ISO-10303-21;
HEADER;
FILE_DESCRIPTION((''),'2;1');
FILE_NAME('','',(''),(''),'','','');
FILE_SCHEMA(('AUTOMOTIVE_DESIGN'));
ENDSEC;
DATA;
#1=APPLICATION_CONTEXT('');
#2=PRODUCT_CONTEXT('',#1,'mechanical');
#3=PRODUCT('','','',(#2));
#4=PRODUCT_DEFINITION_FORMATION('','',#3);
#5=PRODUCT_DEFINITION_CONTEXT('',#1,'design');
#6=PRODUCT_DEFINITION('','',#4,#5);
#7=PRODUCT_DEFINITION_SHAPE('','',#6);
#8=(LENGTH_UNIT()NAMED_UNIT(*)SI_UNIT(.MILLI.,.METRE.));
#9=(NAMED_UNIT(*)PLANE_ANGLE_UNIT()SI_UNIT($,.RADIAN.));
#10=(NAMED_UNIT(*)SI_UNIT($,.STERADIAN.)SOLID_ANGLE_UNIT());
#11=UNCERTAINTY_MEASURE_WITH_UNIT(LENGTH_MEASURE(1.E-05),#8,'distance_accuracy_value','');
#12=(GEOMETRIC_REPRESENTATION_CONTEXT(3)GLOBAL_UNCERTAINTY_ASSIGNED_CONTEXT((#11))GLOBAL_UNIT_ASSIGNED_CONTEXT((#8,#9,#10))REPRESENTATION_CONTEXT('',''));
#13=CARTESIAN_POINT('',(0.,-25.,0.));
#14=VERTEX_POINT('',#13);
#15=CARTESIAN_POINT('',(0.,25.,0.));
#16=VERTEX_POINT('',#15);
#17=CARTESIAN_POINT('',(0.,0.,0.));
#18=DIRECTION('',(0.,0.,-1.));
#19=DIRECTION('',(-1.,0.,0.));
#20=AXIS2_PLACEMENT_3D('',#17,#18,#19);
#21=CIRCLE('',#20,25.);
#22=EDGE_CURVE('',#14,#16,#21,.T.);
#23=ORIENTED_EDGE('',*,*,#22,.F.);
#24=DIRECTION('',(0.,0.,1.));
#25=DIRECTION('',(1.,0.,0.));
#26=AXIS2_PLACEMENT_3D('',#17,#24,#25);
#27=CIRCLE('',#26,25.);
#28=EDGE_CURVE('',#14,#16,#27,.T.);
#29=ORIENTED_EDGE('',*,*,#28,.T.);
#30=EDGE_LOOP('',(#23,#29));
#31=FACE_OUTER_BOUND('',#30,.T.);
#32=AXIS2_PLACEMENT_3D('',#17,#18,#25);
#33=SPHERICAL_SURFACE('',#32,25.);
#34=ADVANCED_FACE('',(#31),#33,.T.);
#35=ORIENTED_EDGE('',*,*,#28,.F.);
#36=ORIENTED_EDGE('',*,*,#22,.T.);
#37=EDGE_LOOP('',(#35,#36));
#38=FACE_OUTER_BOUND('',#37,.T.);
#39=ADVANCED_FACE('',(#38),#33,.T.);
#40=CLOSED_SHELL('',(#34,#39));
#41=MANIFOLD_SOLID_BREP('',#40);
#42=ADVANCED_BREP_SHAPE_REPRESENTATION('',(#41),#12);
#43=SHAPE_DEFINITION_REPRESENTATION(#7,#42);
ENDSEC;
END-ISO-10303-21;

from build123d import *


with BuildPart() as part:
    # 草图1 → 旋转1 (revolve)
    with BuildSketch(Plane.XY):
        with BuildLine():
            Line((0, 25), (0, -25))
            ThreePointArc((0, -25), (25, 0), (0, 25))
        make_face()
    revolve(axis=Axis((0, 25, 0), (0, -1, 0)))


solid = part.part
